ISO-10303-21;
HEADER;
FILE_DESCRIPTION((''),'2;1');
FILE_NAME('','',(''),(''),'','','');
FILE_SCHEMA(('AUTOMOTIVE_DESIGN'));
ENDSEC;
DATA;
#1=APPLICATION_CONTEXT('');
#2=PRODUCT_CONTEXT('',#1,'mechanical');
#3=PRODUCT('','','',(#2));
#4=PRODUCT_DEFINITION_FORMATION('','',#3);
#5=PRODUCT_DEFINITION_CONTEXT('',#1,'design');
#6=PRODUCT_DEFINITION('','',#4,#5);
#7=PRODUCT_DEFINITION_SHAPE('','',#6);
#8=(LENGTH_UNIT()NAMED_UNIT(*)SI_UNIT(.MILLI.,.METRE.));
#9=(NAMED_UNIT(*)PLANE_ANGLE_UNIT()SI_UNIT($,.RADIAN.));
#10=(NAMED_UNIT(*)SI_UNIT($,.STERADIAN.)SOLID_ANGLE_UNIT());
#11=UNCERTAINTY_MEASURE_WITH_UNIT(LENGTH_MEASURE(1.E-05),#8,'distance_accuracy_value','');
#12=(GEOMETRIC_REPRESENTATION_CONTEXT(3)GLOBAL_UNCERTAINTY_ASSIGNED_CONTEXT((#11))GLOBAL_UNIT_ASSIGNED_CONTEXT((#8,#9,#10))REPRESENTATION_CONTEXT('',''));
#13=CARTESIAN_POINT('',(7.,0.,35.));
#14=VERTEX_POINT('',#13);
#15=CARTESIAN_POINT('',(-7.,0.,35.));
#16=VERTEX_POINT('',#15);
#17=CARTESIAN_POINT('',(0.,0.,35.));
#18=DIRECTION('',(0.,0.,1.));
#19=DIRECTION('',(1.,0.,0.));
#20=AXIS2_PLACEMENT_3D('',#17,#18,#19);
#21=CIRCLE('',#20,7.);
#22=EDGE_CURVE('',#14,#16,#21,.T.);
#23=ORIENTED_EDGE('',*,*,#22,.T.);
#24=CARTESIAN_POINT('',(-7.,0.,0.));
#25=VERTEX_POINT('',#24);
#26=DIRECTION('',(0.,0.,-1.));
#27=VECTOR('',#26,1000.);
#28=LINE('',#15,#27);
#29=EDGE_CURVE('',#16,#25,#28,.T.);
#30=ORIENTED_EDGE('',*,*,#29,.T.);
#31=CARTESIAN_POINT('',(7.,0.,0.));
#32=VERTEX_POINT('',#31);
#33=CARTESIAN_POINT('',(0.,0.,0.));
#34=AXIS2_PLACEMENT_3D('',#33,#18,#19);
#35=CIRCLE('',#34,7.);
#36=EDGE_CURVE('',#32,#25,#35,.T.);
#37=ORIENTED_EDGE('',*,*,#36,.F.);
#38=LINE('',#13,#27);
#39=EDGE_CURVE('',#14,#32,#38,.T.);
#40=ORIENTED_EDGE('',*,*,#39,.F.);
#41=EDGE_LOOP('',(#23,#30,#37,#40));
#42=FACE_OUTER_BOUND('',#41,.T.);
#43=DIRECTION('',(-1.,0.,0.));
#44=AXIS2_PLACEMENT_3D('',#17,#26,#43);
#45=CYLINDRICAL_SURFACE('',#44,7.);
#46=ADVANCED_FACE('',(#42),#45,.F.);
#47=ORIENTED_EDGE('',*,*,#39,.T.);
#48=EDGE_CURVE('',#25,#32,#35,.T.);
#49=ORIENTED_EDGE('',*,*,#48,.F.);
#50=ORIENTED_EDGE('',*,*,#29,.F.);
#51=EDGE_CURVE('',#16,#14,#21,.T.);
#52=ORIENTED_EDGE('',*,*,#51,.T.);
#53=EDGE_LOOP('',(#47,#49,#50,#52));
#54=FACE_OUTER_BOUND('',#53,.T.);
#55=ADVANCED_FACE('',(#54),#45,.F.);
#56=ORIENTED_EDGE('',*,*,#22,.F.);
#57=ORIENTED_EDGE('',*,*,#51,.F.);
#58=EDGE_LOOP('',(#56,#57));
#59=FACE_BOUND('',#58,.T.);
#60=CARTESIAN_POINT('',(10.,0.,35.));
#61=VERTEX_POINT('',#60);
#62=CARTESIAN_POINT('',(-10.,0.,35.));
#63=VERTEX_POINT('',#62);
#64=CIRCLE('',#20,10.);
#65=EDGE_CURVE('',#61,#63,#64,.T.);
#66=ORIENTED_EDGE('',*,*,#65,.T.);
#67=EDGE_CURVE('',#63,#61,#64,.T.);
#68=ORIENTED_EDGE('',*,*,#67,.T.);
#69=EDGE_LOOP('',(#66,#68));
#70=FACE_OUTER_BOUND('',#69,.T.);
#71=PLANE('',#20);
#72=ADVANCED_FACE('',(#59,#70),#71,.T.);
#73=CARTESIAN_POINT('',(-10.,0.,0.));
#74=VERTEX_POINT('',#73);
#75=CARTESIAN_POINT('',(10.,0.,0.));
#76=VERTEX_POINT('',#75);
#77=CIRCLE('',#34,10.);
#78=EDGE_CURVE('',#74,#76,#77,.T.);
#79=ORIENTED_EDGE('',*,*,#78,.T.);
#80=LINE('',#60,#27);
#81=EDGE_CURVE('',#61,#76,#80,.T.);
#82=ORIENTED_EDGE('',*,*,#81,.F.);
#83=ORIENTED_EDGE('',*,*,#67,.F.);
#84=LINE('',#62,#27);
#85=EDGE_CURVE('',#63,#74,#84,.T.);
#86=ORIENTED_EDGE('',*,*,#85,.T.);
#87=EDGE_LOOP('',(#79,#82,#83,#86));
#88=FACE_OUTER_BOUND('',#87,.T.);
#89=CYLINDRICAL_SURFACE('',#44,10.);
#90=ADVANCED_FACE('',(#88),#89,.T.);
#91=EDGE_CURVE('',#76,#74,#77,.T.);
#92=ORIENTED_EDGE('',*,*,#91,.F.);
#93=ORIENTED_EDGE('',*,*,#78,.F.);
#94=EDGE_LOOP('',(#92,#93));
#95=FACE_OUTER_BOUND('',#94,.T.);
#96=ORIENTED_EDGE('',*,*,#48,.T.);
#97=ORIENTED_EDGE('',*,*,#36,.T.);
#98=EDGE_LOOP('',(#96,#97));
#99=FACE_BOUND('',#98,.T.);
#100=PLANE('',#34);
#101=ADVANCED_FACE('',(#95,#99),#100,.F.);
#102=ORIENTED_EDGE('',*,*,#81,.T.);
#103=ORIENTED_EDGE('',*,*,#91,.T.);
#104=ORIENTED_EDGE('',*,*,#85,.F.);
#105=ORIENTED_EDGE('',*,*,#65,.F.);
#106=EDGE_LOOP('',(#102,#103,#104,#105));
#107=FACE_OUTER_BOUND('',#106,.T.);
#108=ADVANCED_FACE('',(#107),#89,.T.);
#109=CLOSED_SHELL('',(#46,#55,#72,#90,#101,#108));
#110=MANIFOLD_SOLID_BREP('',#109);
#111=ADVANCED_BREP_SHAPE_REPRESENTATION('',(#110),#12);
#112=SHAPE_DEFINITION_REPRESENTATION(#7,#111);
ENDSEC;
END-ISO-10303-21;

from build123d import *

# Parameters (mm, degrees)
SKETCH1_R           = 10
SKETCH1_R_2         = 7
BOSS_EXTRUDE1_DEPTH = 35


with BuildPart() as part:
    # Sketch1 → Boss-Extrude1 (new body)
    with BuildSketch(Plane.XY):
        Circle(SKETCH1_R)
        Circle(SKETCH1_R_2, mode=Mode.SUBTRACT)
    extrude(amount=BOSS_EXTRUDE1_DEPTH)


solid = part.part
